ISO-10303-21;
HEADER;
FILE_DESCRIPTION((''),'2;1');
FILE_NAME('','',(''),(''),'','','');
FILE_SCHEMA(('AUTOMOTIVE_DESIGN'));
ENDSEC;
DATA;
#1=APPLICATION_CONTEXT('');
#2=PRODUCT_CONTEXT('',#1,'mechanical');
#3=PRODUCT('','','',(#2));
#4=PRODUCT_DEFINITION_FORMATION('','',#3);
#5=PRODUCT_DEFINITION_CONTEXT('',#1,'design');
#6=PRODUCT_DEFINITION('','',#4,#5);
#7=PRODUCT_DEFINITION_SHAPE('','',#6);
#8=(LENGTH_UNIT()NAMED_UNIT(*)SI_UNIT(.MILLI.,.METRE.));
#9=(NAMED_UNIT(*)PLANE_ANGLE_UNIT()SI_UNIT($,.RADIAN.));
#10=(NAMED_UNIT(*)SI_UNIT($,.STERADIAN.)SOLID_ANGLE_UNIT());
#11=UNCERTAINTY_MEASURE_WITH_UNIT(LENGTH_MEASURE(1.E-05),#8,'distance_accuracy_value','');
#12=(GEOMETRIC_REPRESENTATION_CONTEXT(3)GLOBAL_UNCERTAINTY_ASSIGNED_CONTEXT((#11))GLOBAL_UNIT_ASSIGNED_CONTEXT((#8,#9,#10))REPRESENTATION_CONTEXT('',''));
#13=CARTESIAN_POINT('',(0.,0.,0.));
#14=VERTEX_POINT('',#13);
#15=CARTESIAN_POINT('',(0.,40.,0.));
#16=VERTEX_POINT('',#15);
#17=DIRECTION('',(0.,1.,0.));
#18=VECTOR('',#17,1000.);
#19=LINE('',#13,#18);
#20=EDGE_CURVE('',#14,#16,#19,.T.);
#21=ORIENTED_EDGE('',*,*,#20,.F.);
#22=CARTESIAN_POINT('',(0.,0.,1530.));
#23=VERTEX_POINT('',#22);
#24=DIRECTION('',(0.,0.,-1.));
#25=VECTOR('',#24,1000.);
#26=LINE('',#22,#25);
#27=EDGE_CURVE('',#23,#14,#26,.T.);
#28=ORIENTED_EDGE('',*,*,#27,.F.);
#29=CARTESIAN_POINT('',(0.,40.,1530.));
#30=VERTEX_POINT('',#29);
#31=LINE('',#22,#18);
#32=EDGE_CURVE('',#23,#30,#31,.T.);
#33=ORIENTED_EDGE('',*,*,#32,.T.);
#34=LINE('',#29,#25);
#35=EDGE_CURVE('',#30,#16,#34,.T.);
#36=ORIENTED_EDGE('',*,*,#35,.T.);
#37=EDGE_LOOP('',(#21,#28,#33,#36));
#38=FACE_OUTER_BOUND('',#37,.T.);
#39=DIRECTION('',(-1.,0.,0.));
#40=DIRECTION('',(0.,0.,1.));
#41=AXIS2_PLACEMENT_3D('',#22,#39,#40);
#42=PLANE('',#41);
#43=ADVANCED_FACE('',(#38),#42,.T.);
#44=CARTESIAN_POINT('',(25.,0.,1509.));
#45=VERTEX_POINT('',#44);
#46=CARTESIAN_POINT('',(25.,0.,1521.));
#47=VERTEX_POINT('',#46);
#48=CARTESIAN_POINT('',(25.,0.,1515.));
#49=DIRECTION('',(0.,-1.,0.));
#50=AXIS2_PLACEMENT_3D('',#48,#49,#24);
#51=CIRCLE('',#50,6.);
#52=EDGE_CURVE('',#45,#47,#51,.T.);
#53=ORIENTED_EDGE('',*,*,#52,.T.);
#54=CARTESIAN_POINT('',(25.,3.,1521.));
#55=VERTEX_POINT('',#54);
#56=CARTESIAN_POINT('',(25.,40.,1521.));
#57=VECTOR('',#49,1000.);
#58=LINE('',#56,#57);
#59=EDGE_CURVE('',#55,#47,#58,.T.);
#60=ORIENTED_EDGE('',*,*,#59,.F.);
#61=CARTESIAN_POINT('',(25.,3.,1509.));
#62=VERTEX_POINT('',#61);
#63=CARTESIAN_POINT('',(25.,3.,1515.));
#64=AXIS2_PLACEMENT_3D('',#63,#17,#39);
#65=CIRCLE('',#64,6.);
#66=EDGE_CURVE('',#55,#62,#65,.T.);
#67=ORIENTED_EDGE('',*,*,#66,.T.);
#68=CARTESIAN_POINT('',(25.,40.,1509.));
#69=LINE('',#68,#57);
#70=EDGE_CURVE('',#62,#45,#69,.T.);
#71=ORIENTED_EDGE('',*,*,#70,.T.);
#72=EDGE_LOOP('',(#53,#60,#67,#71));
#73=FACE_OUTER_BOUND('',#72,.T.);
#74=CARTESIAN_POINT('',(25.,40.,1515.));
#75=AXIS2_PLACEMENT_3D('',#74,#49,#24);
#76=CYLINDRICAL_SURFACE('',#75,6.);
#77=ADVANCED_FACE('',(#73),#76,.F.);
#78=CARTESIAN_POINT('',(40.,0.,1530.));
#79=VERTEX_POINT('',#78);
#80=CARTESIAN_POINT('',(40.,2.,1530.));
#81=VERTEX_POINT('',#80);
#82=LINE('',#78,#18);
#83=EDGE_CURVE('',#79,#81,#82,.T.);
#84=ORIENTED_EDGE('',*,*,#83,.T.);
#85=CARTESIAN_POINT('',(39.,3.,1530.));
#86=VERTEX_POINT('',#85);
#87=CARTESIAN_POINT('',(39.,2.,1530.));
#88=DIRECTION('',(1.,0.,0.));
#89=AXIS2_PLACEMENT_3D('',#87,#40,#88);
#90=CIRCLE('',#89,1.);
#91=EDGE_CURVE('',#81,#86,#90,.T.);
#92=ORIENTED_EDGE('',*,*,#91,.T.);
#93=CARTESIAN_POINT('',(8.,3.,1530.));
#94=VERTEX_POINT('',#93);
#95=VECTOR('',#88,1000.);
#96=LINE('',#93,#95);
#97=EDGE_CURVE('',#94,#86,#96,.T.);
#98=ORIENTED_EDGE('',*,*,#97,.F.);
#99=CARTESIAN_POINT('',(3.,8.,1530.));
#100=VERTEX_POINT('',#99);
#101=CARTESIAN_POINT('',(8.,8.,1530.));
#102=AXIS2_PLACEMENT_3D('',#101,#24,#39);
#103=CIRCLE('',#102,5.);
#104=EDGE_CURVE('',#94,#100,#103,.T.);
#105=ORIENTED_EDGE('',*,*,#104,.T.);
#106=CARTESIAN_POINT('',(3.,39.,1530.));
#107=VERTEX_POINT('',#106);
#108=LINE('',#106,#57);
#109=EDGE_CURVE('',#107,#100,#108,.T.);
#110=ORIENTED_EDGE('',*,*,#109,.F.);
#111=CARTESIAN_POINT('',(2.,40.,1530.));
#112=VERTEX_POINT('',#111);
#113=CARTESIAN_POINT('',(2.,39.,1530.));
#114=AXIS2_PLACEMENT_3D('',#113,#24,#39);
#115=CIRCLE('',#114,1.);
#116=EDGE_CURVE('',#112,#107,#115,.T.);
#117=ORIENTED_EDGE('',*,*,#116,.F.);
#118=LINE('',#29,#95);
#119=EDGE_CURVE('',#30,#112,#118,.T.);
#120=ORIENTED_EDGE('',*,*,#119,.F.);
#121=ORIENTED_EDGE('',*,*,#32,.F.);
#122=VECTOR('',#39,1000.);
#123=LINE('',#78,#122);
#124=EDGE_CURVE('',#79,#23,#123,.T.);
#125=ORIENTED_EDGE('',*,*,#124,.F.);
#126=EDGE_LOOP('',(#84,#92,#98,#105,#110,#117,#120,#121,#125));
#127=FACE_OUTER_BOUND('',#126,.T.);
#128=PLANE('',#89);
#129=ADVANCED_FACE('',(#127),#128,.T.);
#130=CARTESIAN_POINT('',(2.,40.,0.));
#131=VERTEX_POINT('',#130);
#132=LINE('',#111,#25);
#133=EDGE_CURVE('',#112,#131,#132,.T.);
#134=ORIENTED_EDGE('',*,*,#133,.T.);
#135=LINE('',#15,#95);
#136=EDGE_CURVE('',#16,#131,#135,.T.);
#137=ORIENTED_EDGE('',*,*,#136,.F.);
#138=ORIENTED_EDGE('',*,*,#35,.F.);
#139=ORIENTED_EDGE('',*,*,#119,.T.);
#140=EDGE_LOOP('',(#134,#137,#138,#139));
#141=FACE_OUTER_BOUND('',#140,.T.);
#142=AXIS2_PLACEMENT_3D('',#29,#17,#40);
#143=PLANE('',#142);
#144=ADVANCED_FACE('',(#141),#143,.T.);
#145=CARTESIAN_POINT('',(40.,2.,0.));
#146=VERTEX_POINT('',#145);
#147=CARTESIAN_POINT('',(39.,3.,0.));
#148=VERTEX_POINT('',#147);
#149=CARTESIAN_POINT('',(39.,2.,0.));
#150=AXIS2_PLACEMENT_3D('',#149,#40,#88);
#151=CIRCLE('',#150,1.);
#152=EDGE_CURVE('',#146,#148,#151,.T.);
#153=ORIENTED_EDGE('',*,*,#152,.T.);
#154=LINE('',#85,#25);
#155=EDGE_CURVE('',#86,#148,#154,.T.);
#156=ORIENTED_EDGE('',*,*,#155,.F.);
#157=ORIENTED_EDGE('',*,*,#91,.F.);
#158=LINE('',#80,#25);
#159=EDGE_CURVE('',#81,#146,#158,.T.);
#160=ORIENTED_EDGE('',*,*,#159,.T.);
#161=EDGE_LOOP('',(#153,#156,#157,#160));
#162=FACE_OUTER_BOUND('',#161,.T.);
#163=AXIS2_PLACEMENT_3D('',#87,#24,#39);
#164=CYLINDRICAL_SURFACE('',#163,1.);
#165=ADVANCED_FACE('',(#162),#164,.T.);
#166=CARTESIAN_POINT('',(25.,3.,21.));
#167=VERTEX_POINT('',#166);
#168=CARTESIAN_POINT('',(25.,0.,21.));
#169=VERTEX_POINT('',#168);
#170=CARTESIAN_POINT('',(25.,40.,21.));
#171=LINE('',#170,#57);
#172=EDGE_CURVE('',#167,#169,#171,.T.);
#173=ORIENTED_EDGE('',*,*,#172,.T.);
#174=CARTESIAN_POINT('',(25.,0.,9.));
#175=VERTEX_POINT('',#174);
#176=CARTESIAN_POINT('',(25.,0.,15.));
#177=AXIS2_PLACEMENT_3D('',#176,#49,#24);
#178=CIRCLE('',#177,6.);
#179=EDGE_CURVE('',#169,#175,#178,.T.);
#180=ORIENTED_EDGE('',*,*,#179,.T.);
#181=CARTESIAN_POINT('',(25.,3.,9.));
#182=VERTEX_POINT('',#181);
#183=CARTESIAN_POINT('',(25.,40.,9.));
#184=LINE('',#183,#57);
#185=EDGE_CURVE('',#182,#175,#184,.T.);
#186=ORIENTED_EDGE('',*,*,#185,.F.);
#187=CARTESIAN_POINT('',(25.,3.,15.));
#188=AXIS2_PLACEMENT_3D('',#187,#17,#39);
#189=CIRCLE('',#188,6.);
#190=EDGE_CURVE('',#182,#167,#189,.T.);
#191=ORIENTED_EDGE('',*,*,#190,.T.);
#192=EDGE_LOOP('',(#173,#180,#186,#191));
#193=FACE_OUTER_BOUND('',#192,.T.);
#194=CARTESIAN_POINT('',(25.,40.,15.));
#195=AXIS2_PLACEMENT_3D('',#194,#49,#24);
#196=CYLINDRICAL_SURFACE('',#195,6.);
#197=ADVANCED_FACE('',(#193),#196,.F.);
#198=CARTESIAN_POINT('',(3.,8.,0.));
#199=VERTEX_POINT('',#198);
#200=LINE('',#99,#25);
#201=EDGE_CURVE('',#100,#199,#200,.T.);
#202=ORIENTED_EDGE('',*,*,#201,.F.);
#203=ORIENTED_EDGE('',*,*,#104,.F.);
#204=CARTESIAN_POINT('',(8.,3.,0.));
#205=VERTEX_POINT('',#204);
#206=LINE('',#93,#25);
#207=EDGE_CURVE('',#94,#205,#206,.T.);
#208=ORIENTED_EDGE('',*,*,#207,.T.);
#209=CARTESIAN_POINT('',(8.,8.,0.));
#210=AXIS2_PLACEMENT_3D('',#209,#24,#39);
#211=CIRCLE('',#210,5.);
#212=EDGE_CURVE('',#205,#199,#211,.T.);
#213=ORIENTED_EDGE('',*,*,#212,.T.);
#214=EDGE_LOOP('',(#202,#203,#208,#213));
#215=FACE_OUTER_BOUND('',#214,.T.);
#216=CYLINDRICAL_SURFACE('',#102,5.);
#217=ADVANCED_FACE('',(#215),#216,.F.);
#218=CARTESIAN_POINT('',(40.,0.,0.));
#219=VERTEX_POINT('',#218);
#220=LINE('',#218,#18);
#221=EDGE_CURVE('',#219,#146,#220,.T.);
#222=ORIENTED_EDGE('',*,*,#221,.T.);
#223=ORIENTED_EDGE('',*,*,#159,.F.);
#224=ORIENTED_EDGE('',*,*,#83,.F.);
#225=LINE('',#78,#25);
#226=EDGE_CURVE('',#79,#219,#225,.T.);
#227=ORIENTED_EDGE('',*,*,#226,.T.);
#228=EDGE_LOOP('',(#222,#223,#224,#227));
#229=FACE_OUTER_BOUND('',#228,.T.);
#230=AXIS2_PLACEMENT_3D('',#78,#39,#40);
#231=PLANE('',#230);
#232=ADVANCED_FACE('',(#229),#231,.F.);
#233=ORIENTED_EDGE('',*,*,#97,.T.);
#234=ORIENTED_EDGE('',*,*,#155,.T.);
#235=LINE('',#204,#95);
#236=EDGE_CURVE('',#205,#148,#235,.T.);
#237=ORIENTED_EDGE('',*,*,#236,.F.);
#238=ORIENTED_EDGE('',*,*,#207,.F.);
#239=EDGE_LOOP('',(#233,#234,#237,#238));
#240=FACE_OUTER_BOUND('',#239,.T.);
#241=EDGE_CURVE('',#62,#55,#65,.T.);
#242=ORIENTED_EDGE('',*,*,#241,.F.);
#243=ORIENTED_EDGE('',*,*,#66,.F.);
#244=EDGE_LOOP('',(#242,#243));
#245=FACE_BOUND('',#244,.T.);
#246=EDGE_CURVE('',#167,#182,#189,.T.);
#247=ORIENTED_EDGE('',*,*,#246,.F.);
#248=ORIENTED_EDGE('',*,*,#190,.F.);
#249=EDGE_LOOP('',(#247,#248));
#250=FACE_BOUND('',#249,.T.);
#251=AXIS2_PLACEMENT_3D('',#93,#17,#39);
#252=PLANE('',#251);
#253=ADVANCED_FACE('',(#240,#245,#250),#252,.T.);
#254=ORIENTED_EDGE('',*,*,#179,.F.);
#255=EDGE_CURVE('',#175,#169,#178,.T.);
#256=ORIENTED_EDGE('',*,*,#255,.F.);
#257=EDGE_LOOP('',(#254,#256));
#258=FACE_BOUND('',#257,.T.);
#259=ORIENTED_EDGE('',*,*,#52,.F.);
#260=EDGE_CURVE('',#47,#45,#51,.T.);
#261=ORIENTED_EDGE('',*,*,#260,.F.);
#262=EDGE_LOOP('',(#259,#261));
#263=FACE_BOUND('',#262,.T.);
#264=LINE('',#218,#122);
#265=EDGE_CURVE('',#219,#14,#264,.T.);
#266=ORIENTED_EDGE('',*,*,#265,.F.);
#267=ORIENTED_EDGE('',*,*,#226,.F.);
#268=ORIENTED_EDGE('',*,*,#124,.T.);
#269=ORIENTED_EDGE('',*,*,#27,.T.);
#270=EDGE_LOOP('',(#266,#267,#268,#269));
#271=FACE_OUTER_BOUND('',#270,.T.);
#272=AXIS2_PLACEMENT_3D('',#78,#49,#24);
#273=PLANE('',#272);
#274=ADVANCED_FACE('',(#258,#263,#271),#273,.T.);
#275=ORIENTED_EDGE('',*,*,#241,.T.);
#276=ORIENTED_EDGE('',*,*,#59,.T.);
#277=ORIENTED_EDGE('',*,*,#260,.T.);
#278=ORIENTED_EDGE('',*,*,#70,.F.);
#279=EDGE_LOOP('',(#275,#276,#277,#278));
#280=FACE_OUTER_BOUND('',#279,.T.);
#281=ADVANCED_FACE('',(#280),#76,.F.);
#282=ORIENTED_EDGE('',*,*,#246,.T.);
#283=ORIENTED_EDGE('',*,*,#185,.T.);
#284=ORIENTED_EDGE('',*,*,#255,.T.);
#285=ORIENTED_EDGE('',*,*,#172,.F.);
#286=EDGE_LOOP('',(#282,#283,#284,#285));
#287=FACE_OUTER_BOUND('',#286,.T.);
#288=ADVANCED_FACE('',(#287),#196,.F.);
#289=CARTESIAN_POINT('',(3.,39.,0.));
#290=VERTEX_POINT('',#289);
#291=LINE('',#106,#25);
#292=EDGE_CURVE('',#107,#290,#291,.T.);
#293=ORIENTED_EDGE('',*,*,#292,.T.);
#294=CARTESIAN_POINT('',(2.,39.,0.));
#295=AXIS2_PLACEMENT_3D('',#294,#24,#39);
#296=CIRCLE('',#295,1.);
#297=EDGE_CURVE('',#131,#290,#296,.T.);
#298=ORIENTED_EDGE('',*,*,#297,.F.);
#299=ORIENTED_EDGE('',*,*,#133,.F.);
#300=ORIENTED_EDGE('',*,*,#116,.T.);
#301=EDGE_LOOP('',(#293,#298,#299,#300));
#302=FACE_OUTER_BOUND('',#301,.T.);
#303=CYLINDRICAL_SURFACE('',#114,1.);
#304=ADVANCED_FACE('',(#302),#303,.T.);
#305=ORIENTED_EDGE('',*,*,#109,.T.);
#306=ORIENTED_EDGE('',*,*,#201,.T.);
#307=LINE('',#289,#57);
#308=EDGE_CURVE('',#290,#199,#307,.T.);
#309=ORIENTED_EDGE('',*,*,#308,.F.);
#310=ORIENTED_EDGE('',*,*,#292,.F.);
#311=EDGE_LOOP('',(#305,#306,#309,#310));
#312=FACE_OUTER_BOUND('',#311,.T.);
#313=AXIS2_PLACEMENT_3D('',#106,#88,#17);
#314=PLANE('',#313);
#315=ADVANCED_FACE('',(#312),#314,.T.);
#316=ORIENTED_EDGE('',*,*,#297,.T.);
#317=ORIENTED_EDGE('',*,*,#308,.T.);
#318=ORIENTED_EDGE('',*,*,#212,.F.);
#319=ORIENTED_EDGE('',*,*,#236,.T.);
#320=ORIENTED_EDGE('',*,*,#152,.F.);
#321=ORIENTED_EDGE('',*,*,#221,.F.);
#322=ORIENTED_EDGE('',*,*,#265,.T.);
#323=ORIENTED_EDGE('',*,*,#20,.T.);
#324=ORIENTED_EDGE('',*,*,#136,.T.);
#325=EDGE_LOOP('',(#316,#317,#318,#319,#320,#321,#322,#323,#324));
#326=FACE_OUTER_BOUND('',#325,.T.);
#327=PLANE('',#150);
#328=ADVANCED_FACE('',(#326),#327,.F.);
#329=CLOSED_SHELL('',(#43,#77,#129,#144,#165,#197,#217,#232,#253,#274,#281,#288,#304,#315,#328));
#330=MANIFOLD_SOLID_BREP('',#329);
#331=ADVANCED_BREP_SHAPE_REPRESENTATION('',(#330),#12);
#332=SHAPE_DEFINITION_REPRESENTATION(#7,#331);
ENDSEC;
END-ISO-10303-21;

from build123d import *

# Parameters (mm, degrees)
BOSS_EXTRUDE1_DEPTH = 1530
SKETCH_1_R          = 6
CUT_EXTRUDE1_DEPTH  = 1532.045394494


with BuildPart() as part:
    # Sketch1 → Boss-Extrude1 (new body)
    with BuildSketch(Plane.XY):
        with BuildLine():
            Line((0, 0), (0, 40))
            Line((0, 40), (2, 40))
            ThreePointArc((2, 40), (2.707106781, 39.707106781), (3, 39))
            Line((3, 39), (3, 8))
            ThreePointArc((3, 8), (4.464466094, 4.464466094), (8, 3))
            Line((8, 3), (39, 3))
            ThreePointArc((39, 3), (39.707106781, 2.707106781), (40, 2))
            Line((40, 2), (40, 0))
            Line((40, 0), (0, 0))
        make_face()
    extrude(amount=BOSS_EXTRUDE1_DEPTH)

    # 草图1 → Cut-Extrude1 (cut, through all)
    with BuildSketch(Plane.XZ):
        with Locations(Location((25, 1515, 0), (0, 0, 270))):
            Circle(SKETCH_1_R)
        with Locations(Location((25, 15, 0), (0, 0, 270))):
            Circle(SKETCH_1_R)
    extrude(amount=-CUT_EXTRUDE1_DEPTH, mode=Mode.SUBTRACT)


solid = part.part
